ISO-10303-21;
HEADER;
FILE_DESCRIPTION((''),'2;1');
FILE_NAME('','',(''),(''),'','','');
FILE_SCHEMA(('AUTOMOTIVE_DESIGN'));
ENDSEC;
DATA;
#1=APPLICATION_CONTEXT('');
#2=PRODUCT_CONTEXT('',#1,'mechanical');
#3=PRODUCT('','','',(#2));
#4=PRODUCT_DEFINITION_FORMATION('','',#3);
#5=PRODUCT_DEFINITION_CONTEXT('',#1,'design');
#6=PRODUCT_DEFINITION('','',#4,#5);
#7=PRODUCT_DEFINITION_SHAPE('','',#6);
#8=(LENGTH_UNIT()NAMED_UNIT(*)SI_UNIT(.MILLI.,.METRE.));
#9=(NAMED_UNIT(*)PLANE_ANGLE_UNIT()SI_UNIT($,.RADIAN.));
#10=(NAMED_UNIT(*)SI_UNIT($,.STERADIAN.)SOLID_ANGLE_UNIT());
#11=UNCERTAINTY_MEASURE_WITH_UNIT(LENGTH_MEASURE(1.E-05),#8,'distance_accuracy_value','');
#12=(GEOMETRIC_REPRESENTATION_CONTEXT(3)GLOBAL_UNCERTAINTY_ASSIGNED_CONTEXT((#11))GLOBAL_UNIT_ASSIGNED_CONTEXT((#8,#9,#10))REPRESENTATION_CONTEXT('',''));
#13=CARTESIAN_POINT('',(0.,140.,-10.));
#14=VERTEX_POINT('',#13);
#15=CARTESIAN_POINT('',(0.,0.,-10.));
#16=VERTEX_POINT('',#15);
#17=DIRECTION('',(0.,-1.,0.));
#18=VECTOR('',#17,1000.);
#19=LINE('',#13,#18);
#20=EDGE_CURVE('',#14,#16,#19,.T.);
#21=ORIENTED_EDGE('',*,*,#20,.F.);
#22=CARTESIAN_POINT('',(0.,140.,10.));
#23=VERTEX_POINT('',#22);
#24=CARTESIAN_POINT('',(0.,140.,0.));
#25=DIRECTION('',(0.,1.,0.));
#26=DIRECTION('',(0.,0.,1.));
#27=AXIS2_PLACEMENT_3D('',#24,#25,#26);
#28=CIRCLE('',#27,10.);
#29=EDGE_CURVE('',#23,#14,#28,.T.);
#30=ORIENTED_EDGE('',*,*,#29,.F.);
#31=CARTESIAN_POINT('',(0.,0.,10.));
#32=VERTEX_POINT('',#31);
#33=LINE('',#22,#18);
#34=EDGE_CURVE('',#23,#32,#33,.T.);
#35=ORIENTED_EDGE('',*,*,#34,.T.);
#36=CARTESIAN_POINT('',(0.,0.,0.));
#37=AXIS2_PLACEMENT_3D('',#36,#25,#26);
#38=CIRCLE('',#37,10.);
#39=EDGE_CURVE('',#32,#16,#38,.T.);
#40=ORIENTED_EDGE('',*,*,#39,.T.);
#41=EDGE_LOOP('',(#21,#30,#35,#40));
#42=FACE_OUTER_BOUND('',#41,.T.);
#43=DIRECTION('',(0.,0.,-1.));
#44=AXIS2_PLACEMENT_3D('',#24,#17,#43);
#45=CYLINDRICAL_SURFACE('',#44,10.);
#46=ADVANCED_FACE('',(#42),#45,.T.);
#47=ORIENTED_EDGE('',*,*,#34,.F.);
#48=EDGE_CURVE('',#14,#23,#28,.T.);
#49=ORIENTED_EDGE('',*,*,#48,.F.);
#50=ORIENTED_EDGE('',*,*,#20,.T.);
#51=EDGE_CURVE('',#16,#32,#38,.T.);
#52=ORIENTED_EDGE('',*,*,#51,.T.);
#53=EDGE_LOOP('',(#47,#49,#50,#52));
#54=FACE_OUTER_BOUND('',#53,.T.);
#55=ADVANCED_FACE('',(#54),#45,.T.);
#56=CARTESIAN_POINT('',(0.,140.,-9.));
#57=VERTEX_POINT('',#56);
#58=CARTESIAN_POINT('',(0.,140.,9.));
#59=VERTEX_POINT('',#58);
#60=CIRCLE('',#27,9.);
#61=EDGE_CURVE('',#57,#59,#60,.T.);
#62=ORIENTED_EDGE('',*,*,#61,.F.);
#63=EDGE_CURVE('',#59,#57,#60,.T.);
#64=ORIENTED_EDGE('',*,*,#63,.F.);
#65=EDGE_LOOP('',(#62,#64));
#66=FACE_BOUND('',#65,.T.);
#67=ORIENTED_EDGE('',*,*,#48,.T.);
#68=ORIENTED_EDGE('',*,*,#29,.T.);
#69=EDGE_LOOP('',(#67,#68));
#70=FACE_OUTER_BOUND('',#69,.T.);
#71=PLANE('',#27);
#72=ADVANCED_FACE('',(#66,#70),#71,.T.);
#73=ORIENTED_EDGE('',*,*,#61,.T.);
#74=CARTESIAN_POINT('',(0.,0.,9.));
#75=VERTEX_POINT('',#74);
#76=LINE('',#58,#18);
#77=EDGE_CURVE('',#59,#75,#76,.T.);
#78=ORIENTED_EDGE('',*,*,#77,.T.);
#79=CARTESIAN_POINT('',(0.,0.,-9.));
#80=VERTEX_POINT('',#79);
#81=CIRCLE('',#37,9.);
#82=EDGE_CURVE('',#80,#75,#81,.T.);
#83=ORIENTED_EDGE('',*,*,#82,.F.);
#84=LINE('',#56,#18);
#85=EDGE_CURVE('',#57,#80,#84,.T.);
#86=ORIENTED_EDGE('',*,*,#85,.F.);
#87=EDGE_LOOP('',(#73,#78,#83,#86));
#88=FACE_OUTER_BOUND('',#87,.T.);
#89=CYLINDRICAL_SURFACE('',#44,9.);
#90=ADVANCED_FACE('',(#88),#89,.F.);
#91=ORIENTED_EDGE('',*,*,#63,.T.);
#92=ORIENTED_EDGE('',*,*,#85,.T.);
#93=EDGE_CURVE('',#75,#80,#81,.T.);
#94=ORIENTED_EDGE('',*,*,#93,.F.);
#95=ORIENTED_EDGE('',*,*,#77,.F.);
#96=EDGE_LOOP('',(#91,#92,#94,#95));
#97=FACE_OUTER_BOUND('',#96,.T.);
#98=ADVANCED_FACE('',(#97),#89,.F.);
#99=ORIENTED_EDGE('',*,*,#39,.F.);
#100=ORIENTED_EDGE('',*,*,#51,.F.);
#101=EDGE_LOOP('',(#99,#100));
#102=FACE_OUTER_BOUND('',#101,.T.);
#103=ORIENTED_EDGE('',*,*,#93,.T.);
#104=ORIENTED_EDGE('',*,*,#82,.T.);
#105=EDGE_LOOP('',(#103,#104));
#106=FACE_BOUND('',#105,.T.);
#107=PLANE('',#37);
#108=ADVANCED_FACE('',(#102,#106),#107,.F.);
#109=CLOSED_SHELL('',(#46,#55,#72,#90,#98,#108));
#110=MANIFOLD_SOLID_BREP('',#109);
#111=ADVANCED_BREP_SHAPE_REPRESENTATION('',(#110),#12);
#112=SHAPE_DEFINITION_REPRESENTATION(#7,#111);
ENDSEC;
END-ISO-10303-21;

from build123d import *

# Parameters (mm, degrees)
SKETCH_1_R      = 10
SKETCH_1_R_2    = 9
EXTRUDE_1_DEPTH = 140


with BuildPart() as part:
    # 草图1 → 凸台-拉伸1 (new body)
    with BuildSketch(Plane(origin=(0, 0, 0), x_dir=(1, 0, 0), z_dir=(0, 1, 0))):
        with Locations(Location((0, 0, 0), (0, 0, 270))):
            Circle(SKETCH_1_R)
        with Locations(Location((0, 0, 0), (0, 0, 270))):
            Circle(SKETCH_1_R_2, mode=Mode.SUBTRACT)
    extrude(amount=EXTRUDE_1_DEPTH)


solid = part.part
